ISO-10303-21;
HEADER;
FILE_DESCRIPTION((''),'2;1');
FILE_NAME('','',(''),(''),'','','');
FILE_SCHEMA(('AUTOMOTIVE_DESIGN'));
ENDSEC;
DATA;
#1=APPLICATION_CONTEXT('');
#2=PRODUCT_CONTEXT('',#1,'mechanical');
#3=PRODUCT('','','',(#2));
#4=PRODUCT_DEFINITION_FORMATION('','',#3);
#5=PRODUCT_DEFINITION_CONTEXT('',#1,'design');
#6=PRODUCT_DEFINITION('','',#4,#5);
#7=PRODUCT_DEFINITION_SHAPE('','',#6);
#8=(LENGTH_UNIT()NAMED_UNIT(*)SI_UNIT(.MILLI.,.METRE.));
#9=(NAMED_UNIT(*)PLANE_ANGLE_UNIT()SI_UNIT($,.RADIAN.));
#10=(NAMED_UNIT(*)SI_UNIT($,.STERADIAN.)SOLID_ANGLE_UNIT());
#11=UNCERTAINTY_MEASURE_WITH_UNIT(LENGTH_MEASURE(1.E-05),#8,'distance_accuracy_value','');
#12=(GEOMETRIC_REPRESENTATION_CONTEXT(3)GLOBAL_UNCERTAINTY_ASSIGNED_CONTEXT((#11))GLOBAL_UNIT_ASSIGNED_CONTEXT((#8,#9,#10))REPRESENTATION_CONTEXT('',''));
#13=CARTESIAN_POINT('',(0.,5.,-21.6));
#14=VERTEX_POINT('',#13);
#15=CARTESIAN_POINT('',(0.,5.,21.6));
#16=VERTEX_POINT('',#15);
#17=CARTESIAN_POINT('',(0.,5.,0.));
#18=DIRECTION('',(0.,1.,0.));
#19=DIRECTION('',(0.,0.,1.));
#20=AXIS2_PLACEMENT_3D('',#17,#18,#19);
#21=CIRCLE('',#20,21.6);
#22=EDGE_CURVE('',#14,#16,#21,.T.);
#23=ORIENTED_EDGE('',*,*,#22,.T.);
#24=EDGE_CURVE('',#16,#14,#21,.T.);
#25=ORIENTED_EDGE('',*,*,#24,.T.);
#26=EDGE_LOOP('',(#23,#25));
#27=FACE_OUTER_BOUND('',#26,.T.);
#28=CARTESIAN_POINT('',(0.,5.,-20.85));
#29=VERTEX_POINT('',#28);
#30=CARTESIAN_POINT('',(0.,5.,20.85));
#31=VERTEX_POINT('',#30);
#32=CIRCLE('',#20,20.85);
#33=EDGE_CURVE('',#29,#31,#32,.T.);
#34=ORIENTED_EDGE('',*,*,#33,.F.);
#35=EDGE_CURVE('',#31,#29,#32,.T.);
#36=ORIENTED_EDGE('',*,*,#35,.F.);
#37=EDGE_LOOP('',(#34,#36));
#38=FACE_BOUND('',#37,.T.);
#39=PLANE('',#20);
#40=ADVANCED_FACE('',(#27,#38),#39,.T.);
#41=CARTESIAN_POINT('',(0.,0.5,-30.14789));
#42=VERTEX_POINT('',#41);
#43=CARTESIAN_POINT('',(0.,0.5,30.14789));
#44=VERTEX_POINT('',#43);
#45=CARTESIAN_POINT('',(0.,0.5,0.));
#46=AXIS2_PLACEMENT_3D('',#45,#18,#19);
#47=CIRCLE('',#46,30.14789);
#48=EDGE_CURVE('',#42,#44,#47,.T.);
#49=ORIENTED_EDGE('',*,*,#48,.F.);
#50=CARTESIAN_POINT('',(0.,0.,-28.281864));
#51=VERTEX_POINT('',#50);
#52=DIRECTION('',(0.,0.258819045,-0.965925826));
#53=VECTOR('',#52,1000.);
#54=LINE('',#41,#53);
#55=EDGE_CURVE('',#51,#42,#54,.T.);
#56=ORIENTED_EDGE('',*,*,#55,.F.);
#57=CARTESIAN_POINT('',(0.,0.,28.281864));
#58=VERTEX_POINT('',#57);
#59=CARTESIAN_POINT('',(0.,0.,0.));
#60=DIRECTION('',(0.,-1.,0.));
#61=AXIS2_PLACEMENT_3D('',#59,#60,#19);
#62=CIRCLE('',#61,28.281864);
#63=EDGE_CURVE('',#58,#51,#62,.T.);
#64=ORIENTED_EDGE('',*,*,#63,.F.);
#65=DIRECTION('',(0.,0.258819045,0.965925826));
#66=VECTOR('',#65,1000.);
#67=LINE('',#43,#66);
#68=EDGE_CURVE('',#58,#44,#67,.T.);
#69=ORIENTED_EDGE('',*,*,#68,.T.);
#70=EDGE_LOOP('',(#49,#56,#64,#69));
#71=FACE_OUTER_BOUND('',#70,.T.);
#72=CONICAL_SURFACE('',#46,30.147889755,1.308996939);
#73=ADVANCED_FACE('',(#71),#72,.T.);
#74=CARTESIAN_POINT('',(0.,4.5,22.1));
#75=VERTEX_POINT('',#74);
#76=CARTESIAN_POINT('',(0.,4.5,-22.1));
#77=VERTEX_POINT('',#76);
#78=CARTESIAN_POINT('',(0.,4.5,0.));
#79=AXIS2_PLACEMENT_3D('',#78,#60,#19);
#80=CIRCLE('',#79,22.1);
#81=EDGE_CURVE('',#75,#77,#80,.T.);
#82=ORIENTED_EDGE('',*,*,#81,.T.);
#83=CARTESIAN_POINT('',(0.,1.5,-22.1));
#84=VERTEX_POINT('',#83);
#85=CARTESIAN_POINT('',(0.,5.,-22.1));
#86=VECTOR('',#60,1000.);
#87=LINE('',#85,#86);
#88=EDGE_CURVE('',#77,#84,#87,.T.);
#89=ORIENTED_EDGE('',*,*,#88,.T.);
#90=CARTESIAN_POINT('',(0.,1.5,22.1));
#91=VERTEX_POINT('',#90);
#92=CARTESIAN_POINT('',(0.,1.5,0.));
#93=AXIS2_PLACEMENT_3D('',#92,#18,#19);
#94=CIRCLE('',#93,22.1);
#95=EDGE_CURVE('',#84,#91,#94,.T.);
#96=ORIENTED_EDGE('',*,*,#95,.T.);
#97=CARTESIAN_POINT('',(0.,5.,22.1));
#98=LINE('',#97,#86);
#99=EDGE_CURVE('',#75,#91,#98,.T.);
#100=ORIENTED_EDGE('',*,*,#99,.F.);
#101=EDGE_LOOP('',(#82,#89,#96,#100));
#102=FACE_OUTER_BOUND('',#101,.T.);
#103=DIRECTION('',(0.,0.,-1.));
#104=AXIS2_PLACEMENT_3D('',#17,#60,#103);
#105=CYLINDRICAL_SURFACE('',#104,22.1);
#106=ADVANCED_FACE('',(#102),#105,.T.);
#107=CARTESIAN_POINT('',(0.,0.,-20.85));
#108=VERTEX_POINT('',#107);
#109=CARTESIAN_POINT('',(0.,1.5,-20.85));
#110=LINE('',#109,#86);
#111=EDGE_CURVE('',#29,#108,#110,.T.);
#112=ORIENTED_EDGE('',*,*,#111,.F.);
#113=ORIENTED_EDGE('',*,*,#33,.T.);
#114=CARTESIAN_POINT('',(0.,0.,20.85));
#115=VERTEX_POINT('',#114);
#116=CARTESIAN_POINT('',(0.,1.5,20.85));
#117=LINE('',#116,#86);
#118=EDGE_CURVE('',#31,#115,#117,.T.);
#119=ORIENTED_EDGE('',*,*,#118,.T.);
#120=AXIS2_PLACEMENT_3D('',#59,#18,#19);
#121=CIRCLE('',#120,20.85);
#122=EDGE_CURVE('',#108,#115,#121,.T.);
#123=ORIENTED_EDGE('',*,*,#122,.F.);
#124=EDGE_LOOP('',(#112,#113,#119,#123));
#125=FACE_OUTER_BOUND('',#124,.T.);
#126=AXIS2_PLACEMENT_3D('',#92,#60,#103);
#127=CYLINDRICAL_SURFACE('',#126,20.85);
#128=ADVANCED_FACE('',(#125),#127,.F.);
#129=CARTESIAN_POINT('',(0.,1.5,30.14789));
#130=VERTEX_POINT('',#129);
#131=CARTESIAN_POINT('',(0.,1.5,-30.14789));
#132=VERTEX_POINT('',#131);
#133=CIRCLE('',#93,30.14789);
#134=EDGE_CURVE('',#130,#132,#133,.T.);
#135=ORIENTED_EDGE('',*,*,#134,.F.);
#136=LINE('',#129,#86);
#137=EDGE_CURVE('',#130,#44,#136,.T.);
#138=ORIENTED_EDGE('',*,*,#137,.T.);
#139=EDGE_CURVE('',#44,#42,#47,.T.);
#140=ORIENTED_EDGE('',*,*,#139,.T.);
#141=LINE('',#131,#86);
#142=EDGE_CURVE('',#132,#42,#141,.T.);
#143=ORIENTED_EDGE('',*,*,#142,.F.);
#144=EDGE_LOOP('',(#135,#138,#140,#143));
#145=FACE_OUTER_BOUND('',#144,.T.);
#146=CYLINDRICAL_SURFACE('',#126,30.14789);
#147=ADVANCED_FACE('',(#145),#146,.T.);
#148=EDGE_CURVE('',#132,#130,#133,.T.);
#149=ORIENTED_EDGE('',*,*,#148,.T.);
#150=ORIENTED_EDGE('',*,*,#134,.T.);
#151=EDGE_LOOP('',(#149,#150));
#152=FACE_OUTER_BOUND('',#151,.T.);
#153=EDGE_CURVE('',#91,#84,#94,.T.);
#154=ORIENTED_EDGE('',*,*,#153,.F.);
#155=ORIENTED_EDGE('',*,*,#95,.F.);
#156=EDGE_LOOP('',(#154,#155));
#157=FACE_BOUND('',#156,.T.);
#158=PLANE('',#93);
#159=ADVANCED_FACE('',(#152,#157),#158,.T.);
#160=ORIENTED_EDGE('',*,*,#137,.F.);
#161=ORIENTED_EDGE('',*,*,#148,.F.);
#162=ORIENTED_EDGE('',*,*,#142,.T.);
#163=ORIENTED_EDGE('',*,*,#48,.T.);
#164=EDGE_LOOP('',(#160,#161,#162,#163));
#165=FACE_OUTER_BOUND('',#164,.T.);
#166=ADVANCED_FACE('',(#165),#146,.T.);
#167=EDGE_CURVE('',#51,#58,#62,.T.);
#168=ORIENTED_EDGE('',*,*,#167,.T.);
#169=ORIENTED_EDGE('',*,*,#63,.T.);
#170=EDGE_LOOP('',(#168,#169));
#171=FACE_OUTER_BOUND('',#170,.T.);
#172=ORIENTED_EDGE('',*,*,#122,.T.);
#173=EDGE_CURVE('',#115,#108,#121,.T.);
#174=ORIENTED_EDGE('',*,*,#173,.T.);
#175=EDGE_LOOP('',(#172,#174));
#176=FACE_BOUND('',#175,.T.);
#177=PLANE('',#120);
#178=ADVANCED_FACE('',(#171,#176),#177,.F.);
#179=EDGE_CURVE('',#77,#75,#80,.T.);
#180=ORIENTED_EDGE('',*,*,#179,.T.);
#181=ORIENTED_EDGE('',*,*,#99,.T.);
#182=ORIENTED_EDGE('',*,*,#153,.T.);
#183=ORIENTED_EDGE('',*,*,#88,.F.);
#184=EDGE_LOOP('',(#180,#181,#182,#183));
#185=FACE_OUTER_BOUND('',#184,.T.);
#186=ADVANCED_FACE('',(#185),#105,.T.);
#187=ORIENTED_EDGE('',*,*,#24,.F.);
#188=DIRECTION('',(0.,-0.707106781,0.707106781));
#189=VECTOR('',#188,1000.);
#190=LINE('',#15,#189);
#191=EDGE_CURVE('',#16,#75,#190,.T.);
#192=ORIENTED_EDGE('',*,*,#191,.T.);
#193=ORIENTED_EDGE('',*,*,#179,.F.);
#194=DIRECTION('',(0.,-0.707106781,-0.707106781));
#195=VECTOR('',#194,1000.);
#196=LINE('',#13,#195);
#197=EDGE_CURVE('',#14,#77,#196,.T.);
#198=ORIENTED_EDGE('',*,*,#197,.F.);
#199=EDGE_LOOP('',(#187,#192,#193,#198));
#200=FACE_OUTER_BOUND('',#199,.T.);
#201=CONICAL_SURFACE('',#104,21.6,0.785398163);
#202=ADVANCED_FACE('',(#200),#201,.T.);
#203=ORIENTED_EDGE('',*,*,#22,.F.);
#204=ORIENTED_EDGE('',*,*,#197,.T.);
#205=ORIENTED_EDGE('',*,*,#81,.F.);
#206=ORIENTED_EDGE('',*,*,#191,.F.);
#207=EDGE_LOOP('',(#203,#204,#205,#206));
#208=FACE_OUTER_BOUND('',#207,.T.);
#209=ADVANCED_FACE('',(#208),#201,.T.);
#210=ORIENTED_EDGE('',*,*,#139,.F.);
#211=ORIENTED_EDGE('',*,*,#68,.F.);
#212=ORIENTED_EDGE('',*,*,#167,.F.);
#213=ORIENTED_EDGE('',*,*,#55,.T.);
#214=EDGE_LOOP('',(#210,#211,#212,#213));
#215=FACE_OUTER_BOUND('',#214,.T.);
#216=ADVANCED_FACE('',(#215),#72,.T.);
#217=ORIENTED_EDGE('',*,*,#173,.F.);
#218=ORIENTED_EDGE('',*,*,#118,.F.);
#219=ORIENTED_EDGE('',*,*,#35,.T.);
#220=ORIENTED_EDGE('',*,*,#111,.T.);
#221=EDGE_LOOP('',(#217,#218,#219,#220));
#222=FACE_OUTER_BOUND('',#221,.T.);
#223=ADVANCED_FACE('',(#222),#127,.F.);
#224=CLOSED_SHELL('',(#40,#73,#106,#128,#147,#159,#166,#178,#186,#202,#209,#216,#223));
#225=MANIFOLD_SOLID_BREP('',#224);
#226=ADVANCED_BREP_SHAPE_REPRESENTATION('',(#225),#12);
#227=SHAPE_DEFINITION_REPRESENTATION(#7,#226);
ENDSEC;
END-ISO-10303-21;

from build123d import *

# Parameters (mm, degrees)
SKETCH_1_R          = 30.147889755
SKETCH_1_R_2        = 20.85
EXTRUDE_1_DEPTH     = 1.5
SKETCH_2_R          = 22.1
SKETCH_2_R_2        = 20.85
EXTRUDE_2_DEPTH     = 3.5
CHAMFER_C0_5_1_SIZE = 0.5
CHAMFER_2_SIZE      = 0.5
CHAMFER_2_SIZE2     = 1.866025404


with BuildPart() as part:
    # 草图1 → 凸台-拉伸1 (new body)
    with BuildSketch(Plane(origin=(0, 0, 0), x_dir=(1, 0, 0), z_dir=(0, 1, 0))):
        with Locations(Location((0, 0, 0), (0, 0, 270))):
            Circle(SKETCH_1_R)
        with Locations(Location((0, 0, 0), (0, 0, 270))):
            Circle(SKETCH_1_R_2, mode=Mode.SUBTRACT)
    extrude(amount=EXTRUDE_1_DEPTH)

    # 草图2 → 凸台-拉伸2 (add)
    with BuildSketch(Plane(origin=(0, 1.5, 0), x_dir=(1, 0, 0), z_dir=(0, 1, 0))):
        with Locations(Location((0, 0, 0), (0, 0, 270))):
            Circle(SKETCH_2_R)
        with Locations(Location((0, 0, 0), (0, 0, 270))):
            Circle(SKETCH_2_R_2, mode=Mode.SUBTRACT)
    extrude(amount=EXTRUDE_2_DEPTH)

    # C0.5 倒角1
    chamfer_c0_5_1_edges = [part.edges().sort_by_distance(p)[0] for p in [
        (0, 5, -22.1),
    ]]
    chamfer(chamfer_c0_5_1_edges, length=CHAMFER_C0_5_1_SIZE)

    # 倒角2
    chamfer_2_edges = [part.edges().sort_by_distance(p)[0] for p in [
        (0, 0, -30.147889755),
    ]]
    chamfer_2_side = [part.faces().sort_by_distance(p)[0] for p in [
        (0, 0.75, -30.147889755),
    ]]
    chamfer(chamfer_2_edges, length=CHAMFER_2_SIZE, length2=CHAMFER_2_SIZE2, reference=chamfer_2_side[0])


solid = part.part
